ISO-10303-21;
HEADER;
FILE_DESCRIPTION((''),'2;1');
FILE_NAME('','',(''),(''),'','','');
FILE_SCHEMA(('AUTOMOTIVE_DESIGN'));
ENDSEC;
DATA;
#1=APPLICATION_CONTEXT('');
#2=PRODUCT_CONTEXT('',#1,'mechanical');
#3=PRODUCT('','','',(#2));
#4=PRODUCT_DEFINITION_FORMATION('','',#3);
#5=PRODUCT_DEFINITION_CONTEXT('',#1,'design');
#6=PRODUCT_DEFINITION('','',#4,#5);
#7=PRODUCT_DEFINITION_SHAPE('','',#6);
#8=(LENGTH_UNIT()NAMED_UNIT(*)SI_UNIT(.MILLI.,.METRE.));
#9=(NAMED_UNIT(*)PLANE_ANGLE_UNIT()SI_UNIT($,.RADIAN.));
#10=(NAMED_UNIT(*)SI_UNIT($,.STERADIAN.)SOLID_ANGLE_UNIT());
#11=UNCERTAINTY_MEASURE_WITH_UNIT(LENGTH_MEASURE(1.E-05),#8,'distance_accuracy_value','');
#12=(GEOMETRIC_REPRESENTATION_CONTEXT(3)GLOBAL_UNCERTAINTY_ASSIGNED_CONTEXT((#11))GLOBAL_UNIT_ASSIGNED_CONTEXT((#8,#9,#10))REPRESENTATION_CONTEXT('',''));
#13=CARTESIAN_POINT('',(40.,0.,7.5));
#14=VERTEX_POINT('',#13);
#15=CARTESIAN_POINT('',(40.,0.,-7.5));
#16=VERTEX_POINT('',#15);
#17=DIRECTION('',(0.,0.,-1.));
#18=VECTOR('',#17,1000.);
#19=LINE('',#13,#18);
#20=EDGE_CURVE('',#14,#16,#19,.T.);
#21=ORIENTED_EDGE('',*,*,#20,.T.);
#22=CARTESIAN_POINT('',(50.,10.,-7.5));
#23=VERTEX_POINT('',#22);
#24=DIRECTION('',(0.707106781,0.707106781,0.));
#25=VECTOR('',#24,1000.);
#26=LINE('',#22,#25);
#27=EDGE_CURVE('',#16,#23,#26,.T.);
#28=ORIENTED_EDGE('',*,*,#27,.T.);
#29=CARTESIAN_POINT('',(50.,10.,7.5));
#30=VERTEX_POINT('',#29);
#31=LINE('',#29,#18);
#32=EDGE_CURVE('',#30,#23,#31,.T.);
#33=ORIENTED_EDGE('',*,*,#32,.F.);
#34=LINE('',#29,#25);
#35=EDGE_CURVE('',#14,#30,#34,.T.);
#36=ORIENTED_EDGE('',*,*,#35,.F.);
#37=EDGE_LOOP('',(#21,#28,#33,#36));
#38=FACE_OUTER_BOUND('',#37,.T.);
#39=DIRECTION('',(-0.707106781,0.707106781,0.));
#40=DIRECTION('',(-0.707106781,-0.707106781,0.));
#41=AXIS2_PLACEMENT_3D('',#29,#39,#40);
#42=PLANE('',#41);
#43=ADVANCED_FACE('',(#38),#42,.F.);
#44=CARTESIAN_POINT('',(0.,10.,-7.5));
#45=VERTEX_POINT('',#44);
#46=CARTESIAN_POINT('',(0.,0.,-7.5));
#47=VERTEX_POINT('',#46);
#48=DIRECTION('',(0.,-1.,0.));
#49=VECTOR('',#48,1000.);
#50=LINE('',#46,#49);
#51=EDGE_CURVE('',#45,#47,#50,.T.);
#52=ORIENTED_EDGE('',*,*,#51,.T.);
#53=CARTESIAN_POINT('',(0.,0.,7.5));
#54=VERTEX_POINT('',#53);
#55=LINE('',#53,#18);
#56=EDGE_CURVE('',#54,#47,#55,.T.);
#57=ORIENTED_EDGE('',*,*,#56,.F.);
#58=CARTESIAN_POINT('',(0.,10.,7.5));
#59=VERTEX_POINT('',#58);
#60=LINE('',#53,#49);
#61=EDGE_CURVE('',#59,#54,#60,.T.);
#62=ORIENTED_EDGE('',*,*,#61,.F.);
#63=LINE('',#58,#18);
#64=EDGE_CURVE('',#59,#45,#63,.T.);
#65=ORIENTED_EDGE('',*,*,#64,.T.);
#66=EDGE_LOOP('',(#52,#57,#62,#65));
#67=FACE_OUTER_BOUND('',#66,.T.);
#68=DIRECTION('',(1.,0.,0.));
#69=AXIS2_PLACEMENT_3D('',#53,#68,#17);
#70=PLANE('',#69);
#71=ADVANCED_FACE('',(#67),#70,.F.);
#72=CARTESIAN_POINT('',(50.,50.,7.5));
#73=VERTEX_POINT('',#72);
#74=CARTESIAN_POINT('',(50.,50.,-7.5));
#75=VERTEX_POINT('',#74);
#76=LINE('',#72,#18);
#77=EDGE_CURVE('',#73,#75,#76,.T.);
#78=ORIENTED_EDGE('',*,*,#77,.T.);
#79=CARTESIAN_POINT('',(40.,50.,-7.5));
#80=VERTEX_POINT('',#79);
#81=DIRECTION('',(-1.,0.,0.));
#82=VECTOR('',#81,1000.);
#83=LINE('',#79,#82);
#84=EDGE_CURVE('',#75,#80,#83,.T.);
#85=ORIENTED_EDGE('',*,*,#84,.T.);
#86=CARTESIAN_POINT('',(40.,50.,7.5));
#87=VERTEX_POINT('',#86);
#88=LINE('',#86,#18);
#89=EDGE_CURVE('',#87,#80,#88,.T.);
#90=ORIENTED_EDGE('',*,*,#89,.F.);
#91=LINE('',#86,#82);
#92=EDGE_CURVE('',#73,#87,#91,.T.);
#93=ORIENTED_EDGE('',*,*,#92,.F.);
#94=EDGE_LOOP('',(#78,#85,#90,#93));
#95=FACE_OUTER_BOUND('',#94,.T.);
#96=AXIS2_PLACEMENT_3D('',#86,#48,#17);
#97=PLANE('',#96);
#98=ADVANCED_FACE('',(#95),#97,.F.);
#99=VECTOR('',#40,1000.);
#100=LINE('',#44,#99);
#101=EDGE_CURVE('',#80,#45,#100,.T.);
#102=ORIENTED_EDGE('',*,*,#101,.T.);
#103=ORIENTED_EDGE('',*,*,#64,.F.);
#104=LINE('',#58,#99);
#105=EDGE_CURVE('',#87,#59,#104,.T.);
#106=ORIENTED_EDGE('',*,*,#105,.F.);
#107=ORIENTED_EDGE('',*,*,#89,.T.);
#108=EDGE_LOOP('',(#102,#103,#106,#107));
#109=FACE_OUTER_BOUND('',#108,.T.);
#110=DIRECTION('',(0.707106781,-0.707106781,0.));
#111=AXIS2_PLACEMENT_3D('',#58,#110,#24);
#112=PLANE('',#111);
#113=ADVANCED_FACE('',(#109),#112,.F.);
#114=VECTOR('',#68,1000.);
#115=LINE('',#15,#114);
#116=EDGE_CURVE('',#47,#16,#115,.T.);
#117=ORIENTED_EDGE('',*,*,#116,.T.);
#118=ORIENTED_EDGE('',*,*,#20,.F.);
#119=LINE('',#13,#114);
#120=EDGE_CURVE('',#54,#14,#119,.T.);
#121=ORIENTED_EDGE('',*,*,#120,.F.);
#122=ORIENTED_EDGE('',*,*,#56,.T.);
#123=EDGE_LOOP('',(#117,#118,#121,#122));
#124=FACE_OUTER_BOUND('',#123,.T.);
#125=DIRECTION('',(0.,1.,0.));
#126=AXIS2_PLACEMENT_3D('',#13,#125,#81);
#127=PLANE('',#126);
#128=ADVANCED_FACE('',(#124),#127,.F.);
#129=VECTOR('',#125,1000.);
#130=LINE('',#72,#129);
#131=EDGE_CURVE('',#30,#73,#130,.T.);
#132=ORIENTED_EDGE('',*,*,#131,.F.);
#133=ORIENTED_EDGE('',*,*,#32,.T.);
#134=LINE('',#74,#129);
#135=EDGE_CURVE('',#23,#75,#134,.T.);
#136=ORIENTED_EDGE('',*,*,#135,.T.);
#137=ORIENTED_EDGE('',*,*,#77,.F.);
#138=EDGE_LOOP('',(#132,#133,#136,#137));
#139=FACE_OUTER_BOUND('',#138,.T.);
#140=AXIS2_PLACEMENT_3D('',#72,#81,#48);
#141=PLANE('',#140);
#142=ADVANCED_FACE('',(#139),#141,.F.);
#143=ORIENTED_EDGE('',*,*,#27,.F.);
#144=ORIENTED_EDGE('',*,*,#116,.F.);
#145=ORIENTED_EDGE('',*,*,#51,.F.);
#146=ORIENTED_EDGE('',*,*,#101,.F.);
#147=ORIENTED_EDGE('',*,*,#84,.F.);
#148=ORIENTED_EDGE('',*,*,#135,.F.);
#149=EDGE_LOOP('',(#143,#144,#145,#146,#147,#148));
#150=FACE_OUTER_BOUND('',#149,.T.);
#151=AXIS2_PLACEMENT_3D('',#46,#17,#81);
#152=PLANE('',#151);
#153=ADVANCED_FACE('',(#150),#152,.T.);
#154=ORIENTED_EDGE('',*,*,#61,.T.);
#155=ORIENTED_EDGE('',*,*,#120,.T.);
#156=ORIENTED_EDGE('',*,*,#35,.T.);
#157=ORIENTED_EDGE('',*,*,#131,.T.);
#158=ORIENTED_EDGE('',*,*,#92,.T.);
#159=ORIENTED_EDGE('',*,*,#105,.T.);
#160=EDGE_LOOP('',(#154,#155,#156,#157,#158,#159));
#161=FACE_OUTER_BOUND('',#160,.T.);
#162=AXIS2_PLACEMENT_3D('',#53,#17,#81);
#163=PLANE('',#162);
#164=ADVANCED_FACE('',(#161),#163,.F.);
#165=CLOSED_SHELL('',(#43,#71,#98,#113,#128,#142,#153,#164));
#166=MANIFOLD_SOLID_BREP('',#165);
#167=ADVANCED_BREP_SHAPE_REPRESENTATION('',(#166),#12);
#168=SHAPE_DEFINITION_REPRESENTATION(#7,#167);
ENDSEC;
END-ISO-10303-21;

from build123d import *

# Parameters (mm, degrees)
BOSS_EXTRUDE1_DEPTH = 7.5


with BuildPart() as part:
    # Sketch1 → Boss-Extrude1 (new, symmetric)
    with BuildSketch(Plane.XY):
        Polygon((0, 0), (0, 10), (40, 50), (50, 50), (50, 10), (40, 0), align=None)
    extrude(amount=BOSS_EXTRUDE1_DEPTH, both=True)


solid = part.part
